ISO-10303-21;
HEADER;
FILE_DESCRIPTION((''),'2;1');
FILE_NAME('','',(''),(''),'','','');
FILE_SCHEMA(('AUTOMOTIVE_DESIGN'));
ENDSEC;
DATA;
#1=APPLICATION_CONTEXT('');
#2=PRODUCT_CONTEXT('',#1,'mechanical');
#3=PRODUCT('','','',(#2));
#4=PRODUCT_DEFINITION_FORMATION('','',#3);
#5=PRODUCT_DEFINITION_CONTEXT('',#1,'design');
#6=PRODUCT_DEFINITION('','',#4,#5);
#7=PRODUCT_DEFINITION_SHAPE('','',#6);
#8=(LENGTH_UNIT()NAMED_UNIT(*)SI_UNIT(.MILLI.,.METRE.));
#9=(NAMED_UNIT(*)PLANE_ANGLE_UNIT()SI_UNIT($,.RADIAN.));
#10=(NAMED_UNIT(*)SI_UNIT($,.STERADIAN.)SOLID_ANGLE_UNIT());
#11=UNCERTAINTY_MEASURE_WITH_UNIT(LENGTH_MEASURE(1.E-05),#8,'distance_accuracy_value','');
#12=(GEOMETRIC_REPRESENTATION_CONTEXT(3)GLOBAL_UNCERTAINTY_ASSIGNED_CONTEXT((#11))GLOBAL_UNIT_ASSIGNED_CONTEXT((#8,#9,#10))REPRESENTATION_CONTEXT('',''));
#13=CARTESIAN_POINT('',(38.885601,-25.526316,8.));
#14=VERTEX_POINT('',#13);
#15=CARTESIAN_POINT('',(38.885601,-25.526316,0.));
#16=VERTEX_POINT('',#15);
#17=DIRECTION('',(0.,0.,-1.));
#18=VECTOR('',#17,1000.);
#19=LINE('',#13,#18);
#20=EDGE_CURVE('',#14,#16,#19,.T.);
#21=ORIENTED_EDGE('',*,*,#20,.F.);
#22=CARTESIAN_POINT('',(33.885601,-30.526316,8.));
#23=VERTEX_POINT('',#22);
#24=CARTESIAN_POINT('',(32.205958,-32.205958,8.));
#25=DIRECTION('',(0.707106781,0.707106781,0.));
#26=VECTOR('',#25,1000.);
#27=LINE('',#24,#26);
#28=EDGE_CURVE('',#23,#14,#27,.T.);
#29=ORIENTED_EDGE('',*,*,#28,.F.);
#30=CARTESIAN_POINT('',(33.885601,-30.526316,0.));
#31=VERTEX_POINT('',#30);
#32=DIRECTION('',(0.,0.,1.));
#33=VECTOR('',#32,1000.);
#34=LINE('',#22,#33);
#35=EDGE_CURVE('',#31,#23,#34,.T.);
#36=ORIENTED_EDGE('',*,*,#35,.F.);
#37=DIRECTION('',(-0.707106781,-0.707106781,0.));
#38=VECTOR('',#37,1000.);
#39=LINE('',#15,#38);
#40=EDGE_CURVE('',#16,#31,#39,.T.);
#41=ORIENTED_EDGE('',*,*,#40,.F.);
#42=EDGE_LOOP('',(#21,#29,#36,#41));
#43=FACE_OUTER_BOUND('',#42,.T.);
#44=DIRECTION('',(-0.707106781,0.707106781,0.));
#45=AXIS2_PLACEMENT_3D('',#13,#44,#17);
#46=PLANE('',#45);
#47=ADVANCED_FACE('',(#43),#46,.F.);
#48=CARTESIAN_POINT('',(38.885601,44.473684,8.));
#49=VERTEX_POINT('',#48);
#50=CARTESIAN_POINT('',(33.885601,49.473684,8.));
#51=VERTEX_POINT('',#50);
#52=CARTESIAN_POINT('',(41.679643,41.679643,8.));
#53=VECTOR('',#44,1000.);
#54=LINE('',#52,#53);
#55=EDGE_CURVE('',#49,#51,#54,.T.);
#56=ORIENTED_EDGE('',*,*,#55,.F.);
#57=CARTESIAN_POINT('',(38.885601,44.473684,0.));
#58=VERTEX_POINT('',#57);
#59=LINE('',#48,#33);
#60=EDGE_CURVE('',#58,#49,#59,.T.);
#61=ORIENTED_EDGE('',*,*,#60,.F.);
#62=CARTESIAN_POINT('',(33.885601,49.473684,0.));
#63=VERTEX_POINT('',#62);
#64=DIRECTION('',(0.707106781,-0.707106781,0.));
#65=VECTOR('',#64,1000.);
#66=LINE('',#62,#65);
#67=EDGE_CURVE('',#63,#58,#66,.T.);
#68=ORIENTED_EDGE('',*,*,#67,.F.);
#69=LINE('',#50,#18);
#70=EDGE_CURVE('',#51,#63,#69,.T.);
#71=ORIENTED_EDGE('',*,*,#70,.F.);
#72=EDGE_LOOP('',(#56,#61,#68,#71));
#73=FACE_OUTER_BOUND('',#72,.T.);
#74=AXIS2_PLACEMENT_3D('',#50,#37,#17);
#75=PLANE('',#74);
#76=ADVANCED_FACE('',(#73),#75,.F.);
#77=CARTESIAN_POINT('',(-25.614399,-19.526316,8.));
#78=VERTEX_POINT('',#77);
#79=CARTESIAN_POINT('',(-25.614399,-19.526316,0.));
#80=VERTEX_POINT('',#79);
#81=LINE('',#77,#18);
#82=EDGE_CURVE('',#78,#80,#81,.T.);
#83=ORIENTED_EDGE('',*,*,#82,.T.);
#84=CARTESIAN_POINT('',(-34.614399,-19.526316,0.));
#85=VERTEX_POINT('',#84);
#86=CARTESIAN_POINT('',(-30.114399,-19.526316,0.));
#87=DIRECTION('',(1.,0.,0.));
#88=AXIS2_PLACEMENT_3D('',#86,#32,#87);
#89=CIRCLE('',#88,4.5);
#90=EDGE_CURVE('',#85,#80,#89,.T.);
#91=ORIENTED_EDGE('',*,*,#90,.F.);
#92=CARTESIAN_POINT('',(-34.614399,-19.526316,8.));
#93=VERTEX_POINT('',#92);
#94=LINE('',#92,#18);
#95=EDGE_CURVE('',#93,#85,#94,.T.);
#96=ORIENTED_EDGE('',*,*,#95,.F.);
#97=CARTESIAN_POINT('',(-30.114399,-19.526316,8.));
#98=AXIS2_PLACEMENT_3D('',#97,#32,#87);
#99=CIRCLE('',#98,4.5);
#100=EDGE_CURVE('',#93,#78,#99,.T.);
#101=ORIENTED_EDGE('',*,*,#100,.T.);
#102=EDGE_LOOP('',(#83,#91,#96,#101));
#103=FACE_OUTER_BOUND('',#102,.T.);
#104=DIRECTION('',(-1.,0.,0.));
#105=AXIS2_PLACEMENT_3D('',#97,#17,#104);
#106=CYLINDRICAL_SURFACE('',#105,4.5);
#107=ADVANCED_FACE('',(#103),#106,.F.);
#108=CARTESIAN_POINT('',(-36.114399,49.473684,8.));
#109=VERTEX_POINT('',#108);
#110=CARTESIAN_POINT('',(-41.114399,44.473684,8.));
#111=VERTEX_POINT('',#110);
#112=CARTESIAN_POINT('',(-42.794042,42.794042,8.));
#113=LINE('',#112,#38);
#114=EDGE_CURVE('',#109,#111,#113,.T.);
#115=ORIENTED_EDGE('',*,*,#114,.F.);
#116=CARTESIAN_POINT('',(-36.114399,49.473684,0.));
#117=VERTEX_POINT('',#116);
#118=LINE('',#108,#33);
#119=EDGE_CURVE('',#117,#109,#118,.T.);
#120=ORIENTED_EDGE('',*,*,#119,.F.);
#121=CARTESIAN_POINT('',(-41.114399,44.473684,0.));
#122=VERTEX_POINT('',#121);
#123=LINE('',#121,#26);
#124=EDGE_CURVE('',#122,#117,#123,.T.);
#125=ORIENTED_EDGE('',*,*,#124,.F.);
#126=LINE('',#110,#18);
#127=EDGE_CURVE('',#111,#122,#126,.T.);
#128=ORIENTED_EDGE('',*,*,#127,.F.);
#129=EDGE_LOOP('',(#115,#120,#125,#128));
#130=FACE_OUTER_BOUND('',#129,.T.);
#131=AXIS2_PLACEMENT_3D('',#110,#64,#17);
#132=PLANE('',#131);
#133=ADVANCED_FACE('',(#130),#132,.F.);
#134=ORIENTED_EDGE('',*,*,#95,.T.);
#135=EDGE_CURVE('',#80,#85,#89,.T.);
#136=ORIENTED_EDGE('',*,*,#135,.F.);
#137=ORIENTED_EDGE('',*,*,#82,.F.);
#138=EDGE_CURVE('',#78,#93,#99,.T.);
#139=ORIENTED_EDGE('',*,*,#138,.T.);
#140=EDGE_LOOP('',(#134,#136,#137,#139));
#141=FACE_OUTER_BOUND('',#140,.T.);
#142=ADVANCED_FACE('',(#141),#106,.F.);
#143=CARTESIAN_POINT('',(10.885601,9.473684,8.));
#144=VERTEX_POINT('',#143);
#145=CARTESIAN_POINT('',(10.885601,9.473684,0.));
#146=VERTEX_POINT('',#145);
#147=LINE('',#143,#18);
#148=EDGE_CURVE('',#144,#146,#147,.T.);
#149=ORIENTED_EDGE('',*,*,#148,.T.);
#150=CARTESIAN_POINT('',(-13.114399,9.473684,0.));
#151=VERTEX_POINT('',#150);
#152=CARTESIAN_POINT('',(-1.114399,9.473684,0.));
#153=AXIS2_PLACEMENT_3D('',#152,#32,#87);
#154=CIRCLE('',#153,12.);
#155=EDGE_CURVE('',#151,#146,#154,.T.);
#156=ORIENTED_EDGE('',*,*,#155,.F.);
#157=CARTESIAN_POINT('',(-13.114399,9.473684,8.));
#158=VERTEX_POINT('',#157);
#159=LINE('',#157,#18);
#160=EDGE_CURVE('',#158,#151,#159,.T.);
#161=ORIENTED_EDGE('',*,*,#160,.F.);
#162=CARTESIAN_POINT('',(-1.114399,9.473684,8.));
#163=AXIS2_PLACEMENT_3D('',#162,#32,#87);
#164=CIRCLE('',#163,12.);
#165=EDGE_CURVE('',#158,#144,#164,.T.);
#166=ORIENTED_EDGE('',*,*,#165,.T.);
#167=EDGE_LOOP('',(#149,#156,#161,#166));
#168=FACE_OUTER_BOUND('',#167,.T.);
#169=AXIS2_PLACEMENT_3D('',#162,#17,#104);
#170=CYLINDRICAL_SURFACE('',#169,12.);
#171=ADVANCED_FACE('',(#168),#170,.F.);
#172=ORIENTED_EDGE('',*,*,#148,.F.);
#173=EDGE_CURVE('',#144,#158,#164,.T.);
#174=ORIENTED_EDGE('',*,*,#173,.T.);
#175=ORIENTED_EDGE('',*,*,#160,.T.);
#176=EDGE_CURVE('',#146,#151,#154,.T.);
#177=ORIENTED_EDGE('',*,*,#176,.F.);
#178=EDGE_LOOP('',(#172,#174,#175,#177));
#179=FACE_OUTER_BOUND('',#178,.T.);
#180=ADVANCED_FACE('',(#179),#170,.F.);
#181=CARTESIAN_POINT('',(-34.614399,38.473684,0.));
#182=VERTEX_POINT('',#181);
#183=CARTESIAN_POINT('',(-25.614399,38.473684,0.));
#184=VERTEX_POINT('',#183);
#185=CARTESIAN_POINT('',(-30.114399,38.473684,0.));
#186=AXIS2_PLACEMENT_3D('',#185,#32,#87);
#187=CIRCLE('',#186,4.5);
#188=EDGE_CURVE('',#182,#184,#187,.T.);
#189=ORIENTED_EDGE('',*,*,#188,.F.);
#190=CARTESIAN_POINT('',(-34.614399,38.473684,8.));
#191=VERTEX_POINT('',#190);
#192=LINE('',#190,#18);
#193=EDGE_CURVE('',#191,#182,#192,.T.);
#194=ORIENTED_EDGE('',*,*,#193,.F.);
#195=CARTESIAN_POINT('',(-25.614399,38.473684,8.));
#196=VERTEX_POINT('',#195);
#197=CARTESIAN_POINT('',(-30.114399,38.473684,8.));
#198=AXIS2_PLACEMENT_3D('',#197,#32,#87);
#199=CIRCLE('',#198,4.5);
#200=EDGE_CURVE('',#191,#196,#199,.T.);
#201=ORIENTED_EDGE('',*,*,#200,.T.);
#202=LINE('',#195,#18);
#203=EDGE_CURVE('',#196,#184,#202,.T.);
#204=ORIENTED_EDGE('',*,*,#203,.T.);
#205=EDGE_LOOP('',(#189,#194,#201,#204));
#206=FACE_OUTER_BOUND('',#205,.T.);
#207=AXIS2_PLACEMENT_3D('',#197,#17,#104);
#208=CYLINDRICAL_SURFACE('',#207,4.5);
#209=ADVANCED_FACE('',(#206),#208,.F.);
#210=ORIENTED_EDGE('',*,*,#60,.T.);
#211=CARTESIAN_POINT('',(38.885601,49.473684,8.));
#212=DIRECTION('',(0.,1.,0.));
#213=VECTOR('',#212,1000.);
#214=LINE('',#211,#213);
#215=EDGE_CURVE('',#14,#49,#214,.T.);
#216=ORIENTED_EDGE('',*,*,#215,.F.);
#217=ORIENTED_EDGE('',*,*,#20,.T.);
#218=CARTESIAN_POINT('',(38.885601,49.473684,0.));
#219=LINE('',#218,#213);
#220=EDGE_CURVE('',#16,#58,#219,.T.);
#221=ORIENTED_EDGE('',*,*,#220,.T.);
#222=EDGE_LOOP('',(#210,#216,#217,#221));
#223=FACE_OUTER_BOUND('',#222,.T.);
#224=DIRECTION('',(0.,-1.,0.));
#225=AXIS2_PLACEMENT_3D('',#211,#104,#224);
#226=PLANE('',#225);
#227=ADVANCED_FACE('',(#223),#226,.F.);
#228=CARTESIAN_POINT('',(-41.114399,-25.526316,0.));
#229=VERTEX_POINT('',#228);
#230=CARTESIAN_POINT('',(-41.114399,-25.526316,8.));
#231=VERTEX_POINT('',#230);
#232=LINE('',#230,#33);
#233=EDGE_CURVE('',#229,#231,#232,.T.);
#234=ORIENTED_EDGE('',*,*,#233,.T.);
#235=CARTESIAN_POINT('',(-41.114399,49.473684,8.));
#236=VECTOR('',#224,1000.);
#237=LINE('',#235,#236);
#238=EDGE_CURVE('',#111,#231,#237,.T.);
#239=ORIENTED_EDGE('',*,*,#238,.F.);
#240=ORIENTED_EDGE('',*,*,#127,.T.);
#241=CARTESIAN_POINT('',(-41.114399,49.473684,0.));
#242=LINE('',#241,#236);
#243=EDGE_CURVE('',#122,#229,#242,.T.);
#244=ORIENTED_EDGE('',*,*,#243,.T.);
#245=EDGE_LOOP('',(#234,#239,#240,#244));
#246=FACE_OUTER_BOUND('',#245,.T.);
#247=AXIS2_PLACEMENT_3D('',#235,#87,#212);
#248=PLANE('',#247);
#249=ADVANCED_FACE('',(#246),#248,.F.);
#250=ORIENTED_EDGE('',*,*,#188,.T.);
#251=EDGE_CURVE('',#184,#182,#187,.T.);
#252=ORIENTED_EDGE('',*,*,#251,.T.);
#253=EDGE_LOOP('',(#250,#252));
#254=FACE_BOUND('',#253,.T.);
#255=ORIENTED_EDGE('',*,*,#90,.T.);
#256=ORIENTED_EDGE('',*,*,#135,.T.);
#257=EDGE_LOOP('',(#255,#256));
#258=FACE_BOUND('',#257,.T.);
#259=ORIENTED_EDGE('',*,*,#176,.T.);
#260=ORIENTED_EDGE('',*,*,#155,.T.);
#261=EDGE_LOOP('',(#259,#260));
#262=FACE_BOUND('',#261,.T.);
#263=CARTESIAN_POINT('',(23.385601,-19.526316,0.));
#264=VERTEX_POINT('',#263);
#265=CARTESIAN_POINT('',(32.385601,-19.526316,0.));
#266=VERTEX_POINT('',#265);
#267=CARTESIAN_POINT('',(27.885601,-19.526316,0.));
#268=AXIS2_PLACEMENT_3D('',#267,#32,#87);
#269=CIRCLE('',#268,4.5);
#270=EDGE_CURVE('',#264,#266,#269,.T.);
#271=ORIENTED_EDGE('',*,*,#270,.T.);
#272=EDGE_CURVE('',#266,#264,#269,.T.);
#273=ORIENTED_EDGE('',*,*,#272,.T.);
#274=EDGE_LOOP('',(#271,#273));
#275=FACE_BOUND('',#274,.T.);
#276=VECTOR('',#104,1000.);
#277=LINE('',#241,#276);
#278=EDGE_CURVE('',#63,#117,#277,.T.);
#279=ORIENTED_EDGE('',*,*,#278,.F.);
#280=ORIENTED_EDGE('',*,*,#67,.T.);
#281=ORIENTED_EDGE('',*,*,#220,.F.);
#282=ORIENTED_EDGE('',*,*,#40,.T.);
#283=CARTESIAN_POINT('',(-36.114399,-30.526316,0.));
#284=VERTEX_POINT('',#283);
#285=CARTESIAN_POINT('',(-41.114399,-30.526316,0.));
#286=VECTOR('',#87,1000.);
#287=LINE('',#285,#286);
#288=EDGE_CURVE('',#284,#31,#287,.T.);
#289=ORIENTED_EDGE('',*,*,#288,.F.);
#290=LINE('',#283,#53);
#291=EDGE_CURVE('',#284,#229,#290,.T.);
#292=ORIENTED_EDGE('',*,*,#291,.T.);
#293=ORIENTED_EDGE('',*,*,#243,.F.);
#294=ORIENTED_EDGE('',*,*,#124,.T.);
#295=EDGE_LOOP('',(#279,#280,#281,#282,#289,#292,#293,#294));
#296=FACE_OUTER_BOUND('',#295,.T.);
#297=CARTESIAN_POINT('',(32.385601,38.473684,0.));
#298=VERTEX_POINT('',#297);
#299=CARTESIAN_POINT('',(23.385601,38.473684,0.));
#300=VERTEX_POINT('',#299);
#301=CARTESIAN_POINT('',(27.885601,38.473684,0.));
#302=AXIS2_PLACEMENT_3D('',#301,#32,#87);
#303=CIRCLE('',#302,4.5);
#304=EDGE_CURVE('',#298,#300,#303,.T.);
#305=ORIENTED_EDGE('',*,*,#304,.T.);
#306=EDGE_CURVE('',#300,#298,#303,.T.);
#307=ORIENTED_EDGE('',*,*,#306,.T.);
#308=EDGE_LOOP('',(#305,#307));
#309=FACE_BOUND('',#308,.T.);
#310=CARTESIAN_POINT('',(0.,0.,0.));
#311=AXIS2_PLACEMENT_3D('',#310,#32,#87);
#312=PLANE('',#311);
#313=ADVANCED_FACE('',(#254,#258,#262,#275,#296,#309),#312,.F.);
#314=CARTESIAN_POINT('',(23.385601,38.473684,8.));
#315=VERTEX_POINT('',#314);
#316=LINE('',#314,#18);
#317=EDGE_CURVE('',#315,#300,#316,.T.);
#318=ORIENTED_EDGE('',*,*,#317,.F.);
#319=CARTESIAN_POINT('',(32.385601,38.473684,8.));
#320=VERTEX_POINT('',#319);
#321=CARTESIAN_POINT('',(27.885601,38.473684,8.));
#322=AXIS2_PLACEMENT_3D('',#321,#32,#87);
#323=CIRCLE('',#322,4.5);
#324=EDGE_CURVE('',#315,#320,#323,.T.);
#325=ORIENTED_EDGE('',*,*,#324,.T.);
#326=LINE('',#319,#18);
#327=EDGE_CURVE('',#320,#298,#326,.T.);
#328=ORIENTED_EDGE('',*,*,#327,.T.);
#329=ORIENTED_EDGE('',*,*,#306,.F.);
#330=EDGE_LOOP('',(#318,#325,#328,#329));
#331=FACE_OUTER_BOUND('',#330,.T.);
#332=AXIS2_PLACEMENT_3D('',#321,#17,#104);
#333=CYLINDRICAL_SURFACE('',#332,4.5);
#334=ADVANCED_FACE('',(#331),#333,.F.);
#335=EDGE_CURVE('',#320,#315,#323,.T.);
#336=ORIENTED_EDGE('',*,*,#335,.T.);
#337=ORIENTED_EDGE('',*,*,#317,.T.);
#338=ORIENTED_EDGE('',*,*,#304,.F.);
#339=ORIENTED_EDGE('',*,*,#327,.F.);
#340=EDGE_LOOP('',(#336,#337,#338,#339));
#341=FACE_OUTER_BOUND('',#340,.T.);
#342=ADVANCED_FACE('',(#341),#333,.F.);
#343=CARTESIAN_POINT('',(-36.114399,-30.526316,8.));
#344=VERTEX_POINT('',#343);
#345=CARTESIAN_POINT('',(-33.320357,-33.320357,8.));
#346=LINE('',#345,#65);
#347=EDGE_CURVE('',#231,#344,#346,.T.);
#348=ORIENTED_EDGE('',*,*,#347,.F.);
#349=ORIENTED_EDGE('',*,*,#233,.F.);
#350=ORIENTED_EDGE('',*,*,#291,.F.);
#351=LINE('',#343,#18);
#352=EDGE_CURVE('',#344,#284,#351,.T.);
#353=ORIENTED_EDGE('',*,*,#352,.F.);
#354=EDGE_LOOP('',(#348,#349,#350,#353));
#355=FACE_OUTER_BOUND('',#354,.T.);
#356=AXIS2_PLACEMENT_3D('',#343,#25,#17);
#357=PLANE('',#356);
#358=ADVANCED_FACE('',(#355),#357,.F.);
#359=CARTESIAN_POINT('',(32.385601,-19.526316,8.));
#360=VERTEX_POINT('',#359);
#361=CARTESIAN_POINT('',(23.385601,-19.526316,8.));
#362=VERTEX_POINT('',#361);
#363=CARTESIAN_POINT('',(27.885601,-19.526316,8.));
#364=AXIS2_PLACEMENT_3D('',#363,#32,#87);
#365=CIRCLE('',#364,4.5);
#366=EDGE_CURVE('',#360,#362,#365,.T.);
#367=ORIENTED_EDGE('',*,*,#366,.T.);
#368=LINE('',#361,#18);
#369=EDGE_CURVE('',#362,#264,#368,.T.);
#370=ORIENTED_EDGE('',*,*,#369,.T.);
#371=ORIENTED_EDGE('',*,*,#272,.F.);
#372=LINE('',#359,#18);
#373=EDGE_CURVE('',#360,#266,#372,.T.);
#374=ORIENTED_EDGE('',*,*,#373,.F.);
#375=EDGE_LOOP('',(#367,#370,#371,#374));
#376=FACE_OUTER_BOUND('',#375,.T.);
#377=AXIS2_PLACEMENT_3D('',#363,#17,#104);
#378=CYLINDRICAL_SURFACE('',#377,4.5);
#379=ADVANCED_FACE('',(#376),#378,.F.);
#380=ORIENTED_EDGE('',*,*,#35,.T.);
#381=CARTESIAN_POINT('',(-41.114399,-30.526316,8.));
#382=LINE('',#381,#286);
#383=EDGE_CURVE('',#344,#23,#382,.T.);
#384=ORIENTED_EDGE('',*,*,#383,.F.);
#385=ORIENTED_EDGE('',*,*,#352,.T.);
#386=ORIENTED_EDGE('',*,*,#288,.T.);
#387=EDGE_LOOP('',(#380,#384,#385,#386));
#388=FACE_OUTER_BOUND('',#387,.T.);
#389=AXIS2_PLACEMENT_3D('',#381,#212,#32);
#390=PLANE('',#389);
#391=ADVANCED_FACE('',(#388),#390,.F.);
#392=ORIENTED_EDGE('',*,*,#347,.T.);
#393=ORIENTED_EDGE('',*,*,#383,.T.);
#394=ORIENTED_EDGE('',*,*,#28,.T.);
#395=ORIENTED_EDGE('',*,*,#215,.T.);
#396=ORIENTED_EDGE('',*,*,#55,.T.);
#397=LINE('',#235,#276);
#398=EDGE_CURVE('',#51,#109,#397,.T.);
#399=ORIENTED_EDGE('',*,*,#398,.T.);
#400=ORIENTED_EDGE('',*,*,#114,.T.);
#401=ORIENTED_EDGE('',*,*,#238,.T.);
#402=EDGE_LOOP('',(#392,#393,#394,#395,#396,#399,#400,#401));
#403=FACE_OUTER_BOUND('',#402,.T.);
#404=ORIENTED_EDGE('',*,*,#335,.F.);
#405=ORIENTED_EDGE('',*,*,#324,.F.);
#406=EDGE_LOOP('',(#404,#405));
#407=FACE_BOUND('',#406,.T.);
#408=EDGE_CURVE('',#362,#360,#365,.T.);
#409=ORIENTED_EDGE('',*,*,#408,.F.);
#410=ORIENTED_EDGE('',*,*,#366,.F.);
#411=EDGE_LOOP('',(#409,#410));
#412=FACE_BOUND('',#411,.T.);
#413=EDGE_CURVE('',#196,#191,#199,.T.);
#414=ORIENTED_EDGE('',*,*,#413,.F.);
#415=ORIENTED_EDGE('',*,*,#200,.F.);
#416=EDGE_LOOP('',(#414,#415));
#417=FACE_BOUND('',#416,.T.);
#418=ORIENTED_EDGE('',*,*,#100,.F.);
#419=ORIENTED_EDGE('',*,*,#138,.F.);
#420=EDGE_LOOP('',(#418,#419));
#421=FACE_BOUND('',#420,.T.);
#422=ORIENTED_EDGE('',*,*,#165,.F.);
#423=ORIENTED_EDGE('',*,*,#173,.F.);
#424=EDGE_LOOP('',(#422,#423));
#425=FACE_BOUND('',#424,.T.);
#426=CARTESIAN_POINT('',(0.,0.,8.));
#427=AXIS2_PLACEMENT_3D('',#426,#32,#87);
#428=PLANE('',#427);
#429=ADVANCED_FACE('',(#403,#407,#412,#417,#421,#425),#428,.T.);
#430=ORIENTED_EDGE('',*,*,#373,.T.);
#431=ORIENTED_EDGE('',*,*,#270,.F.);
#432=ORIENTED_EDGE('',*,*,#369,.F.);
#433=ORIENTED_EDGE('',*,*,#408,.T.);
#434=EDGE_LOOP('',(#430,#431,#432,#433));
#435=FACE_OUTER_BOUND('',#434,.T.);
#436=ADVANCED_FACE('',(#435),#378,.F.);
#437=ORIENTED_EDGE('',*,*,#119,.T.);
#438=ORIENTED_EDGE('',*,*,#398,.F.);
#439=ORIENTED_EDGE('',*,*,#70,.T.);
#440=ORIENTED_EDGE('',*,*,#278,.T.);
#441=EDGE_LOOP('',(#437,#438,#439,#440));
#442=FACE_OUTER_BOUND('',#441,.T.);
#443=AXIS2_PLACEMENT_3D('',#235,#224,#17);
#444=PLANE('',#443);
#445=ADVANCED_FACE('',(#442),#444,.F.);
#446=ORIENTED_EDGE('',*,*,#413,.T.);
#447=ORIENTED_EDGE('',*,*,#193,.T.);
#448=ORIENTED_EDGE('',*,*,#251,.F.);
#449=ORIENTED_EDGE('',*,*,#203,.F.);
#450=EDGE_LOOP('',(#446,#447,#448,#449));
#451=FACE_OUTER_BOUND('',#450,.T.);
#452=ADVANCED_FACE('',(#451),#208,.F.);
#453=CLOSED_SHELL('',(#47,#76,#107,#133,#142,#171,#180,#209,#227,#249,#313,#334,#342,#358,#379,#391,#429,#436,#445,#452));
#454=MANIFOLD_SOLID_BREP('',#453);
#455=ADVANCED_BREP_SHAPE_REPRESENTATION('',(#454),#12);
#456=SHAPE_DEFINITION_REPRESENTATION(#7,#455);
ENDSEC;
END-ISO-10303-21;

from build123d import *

# Parameters (mm, degrees)
SKETCH1_W           = 80
SKETCH1_H           = 80
SKETCH1_R           = 12
SKETCH1_R_2         = 4.5
BOSS_EXTRUDE1_DEPTH = 8
CHAMFER1_SIZE       = 5


with BuildPart() as part:
    # Sketch1 → Boss-Extrude1 (new body)
    with BuildSketch(Plane.XY):
        with Locations((-1.114398958, 9.473684211)):
            Rectangle(SKETCH1_W, SKETCH1_H)
        with Locations((-1.114398958, 9.473684211)):
            Circle(SKETCH1_R, mode=Mode.SUBTRACT)
        with Locations((-30.114398958, 38.473684211)):
            Circle(SKETCH1_R_2, mode=Mode.SUBTRACT)
        with Locations((-30.114398958, -19.526315789)):
            Circle(SKETCH1_R_2, mode=Mode.SUBTRACT)
        with Locations((27.885601042, -19.526315789)):
            Circle(SKETCH1_R_2, mode=Mode.SUBTRACT)
        with Locations((27.885601042, 38.473684211)):
            Circle(SKETCH1_R_2, mode=Mode.SUBTRACT)
    extrude(amount=BOSS_EXTRUDE1_DEPTH)

    # Chamfer1
    chamfer1_edges = [part.edges().sort_by_distance(p)[0] for p in [
        (-41.114398958, 49.473684211, 4),
        (38.885601042, 49.473684211, 4),
        (38.885601042, -30.526315789, 4),
        (-41.114398958, -30.526315789, 4),
    ]]
    chamfer(chamfer1_edges, length=CHAMFER1_SIZE)


solid = part.part
